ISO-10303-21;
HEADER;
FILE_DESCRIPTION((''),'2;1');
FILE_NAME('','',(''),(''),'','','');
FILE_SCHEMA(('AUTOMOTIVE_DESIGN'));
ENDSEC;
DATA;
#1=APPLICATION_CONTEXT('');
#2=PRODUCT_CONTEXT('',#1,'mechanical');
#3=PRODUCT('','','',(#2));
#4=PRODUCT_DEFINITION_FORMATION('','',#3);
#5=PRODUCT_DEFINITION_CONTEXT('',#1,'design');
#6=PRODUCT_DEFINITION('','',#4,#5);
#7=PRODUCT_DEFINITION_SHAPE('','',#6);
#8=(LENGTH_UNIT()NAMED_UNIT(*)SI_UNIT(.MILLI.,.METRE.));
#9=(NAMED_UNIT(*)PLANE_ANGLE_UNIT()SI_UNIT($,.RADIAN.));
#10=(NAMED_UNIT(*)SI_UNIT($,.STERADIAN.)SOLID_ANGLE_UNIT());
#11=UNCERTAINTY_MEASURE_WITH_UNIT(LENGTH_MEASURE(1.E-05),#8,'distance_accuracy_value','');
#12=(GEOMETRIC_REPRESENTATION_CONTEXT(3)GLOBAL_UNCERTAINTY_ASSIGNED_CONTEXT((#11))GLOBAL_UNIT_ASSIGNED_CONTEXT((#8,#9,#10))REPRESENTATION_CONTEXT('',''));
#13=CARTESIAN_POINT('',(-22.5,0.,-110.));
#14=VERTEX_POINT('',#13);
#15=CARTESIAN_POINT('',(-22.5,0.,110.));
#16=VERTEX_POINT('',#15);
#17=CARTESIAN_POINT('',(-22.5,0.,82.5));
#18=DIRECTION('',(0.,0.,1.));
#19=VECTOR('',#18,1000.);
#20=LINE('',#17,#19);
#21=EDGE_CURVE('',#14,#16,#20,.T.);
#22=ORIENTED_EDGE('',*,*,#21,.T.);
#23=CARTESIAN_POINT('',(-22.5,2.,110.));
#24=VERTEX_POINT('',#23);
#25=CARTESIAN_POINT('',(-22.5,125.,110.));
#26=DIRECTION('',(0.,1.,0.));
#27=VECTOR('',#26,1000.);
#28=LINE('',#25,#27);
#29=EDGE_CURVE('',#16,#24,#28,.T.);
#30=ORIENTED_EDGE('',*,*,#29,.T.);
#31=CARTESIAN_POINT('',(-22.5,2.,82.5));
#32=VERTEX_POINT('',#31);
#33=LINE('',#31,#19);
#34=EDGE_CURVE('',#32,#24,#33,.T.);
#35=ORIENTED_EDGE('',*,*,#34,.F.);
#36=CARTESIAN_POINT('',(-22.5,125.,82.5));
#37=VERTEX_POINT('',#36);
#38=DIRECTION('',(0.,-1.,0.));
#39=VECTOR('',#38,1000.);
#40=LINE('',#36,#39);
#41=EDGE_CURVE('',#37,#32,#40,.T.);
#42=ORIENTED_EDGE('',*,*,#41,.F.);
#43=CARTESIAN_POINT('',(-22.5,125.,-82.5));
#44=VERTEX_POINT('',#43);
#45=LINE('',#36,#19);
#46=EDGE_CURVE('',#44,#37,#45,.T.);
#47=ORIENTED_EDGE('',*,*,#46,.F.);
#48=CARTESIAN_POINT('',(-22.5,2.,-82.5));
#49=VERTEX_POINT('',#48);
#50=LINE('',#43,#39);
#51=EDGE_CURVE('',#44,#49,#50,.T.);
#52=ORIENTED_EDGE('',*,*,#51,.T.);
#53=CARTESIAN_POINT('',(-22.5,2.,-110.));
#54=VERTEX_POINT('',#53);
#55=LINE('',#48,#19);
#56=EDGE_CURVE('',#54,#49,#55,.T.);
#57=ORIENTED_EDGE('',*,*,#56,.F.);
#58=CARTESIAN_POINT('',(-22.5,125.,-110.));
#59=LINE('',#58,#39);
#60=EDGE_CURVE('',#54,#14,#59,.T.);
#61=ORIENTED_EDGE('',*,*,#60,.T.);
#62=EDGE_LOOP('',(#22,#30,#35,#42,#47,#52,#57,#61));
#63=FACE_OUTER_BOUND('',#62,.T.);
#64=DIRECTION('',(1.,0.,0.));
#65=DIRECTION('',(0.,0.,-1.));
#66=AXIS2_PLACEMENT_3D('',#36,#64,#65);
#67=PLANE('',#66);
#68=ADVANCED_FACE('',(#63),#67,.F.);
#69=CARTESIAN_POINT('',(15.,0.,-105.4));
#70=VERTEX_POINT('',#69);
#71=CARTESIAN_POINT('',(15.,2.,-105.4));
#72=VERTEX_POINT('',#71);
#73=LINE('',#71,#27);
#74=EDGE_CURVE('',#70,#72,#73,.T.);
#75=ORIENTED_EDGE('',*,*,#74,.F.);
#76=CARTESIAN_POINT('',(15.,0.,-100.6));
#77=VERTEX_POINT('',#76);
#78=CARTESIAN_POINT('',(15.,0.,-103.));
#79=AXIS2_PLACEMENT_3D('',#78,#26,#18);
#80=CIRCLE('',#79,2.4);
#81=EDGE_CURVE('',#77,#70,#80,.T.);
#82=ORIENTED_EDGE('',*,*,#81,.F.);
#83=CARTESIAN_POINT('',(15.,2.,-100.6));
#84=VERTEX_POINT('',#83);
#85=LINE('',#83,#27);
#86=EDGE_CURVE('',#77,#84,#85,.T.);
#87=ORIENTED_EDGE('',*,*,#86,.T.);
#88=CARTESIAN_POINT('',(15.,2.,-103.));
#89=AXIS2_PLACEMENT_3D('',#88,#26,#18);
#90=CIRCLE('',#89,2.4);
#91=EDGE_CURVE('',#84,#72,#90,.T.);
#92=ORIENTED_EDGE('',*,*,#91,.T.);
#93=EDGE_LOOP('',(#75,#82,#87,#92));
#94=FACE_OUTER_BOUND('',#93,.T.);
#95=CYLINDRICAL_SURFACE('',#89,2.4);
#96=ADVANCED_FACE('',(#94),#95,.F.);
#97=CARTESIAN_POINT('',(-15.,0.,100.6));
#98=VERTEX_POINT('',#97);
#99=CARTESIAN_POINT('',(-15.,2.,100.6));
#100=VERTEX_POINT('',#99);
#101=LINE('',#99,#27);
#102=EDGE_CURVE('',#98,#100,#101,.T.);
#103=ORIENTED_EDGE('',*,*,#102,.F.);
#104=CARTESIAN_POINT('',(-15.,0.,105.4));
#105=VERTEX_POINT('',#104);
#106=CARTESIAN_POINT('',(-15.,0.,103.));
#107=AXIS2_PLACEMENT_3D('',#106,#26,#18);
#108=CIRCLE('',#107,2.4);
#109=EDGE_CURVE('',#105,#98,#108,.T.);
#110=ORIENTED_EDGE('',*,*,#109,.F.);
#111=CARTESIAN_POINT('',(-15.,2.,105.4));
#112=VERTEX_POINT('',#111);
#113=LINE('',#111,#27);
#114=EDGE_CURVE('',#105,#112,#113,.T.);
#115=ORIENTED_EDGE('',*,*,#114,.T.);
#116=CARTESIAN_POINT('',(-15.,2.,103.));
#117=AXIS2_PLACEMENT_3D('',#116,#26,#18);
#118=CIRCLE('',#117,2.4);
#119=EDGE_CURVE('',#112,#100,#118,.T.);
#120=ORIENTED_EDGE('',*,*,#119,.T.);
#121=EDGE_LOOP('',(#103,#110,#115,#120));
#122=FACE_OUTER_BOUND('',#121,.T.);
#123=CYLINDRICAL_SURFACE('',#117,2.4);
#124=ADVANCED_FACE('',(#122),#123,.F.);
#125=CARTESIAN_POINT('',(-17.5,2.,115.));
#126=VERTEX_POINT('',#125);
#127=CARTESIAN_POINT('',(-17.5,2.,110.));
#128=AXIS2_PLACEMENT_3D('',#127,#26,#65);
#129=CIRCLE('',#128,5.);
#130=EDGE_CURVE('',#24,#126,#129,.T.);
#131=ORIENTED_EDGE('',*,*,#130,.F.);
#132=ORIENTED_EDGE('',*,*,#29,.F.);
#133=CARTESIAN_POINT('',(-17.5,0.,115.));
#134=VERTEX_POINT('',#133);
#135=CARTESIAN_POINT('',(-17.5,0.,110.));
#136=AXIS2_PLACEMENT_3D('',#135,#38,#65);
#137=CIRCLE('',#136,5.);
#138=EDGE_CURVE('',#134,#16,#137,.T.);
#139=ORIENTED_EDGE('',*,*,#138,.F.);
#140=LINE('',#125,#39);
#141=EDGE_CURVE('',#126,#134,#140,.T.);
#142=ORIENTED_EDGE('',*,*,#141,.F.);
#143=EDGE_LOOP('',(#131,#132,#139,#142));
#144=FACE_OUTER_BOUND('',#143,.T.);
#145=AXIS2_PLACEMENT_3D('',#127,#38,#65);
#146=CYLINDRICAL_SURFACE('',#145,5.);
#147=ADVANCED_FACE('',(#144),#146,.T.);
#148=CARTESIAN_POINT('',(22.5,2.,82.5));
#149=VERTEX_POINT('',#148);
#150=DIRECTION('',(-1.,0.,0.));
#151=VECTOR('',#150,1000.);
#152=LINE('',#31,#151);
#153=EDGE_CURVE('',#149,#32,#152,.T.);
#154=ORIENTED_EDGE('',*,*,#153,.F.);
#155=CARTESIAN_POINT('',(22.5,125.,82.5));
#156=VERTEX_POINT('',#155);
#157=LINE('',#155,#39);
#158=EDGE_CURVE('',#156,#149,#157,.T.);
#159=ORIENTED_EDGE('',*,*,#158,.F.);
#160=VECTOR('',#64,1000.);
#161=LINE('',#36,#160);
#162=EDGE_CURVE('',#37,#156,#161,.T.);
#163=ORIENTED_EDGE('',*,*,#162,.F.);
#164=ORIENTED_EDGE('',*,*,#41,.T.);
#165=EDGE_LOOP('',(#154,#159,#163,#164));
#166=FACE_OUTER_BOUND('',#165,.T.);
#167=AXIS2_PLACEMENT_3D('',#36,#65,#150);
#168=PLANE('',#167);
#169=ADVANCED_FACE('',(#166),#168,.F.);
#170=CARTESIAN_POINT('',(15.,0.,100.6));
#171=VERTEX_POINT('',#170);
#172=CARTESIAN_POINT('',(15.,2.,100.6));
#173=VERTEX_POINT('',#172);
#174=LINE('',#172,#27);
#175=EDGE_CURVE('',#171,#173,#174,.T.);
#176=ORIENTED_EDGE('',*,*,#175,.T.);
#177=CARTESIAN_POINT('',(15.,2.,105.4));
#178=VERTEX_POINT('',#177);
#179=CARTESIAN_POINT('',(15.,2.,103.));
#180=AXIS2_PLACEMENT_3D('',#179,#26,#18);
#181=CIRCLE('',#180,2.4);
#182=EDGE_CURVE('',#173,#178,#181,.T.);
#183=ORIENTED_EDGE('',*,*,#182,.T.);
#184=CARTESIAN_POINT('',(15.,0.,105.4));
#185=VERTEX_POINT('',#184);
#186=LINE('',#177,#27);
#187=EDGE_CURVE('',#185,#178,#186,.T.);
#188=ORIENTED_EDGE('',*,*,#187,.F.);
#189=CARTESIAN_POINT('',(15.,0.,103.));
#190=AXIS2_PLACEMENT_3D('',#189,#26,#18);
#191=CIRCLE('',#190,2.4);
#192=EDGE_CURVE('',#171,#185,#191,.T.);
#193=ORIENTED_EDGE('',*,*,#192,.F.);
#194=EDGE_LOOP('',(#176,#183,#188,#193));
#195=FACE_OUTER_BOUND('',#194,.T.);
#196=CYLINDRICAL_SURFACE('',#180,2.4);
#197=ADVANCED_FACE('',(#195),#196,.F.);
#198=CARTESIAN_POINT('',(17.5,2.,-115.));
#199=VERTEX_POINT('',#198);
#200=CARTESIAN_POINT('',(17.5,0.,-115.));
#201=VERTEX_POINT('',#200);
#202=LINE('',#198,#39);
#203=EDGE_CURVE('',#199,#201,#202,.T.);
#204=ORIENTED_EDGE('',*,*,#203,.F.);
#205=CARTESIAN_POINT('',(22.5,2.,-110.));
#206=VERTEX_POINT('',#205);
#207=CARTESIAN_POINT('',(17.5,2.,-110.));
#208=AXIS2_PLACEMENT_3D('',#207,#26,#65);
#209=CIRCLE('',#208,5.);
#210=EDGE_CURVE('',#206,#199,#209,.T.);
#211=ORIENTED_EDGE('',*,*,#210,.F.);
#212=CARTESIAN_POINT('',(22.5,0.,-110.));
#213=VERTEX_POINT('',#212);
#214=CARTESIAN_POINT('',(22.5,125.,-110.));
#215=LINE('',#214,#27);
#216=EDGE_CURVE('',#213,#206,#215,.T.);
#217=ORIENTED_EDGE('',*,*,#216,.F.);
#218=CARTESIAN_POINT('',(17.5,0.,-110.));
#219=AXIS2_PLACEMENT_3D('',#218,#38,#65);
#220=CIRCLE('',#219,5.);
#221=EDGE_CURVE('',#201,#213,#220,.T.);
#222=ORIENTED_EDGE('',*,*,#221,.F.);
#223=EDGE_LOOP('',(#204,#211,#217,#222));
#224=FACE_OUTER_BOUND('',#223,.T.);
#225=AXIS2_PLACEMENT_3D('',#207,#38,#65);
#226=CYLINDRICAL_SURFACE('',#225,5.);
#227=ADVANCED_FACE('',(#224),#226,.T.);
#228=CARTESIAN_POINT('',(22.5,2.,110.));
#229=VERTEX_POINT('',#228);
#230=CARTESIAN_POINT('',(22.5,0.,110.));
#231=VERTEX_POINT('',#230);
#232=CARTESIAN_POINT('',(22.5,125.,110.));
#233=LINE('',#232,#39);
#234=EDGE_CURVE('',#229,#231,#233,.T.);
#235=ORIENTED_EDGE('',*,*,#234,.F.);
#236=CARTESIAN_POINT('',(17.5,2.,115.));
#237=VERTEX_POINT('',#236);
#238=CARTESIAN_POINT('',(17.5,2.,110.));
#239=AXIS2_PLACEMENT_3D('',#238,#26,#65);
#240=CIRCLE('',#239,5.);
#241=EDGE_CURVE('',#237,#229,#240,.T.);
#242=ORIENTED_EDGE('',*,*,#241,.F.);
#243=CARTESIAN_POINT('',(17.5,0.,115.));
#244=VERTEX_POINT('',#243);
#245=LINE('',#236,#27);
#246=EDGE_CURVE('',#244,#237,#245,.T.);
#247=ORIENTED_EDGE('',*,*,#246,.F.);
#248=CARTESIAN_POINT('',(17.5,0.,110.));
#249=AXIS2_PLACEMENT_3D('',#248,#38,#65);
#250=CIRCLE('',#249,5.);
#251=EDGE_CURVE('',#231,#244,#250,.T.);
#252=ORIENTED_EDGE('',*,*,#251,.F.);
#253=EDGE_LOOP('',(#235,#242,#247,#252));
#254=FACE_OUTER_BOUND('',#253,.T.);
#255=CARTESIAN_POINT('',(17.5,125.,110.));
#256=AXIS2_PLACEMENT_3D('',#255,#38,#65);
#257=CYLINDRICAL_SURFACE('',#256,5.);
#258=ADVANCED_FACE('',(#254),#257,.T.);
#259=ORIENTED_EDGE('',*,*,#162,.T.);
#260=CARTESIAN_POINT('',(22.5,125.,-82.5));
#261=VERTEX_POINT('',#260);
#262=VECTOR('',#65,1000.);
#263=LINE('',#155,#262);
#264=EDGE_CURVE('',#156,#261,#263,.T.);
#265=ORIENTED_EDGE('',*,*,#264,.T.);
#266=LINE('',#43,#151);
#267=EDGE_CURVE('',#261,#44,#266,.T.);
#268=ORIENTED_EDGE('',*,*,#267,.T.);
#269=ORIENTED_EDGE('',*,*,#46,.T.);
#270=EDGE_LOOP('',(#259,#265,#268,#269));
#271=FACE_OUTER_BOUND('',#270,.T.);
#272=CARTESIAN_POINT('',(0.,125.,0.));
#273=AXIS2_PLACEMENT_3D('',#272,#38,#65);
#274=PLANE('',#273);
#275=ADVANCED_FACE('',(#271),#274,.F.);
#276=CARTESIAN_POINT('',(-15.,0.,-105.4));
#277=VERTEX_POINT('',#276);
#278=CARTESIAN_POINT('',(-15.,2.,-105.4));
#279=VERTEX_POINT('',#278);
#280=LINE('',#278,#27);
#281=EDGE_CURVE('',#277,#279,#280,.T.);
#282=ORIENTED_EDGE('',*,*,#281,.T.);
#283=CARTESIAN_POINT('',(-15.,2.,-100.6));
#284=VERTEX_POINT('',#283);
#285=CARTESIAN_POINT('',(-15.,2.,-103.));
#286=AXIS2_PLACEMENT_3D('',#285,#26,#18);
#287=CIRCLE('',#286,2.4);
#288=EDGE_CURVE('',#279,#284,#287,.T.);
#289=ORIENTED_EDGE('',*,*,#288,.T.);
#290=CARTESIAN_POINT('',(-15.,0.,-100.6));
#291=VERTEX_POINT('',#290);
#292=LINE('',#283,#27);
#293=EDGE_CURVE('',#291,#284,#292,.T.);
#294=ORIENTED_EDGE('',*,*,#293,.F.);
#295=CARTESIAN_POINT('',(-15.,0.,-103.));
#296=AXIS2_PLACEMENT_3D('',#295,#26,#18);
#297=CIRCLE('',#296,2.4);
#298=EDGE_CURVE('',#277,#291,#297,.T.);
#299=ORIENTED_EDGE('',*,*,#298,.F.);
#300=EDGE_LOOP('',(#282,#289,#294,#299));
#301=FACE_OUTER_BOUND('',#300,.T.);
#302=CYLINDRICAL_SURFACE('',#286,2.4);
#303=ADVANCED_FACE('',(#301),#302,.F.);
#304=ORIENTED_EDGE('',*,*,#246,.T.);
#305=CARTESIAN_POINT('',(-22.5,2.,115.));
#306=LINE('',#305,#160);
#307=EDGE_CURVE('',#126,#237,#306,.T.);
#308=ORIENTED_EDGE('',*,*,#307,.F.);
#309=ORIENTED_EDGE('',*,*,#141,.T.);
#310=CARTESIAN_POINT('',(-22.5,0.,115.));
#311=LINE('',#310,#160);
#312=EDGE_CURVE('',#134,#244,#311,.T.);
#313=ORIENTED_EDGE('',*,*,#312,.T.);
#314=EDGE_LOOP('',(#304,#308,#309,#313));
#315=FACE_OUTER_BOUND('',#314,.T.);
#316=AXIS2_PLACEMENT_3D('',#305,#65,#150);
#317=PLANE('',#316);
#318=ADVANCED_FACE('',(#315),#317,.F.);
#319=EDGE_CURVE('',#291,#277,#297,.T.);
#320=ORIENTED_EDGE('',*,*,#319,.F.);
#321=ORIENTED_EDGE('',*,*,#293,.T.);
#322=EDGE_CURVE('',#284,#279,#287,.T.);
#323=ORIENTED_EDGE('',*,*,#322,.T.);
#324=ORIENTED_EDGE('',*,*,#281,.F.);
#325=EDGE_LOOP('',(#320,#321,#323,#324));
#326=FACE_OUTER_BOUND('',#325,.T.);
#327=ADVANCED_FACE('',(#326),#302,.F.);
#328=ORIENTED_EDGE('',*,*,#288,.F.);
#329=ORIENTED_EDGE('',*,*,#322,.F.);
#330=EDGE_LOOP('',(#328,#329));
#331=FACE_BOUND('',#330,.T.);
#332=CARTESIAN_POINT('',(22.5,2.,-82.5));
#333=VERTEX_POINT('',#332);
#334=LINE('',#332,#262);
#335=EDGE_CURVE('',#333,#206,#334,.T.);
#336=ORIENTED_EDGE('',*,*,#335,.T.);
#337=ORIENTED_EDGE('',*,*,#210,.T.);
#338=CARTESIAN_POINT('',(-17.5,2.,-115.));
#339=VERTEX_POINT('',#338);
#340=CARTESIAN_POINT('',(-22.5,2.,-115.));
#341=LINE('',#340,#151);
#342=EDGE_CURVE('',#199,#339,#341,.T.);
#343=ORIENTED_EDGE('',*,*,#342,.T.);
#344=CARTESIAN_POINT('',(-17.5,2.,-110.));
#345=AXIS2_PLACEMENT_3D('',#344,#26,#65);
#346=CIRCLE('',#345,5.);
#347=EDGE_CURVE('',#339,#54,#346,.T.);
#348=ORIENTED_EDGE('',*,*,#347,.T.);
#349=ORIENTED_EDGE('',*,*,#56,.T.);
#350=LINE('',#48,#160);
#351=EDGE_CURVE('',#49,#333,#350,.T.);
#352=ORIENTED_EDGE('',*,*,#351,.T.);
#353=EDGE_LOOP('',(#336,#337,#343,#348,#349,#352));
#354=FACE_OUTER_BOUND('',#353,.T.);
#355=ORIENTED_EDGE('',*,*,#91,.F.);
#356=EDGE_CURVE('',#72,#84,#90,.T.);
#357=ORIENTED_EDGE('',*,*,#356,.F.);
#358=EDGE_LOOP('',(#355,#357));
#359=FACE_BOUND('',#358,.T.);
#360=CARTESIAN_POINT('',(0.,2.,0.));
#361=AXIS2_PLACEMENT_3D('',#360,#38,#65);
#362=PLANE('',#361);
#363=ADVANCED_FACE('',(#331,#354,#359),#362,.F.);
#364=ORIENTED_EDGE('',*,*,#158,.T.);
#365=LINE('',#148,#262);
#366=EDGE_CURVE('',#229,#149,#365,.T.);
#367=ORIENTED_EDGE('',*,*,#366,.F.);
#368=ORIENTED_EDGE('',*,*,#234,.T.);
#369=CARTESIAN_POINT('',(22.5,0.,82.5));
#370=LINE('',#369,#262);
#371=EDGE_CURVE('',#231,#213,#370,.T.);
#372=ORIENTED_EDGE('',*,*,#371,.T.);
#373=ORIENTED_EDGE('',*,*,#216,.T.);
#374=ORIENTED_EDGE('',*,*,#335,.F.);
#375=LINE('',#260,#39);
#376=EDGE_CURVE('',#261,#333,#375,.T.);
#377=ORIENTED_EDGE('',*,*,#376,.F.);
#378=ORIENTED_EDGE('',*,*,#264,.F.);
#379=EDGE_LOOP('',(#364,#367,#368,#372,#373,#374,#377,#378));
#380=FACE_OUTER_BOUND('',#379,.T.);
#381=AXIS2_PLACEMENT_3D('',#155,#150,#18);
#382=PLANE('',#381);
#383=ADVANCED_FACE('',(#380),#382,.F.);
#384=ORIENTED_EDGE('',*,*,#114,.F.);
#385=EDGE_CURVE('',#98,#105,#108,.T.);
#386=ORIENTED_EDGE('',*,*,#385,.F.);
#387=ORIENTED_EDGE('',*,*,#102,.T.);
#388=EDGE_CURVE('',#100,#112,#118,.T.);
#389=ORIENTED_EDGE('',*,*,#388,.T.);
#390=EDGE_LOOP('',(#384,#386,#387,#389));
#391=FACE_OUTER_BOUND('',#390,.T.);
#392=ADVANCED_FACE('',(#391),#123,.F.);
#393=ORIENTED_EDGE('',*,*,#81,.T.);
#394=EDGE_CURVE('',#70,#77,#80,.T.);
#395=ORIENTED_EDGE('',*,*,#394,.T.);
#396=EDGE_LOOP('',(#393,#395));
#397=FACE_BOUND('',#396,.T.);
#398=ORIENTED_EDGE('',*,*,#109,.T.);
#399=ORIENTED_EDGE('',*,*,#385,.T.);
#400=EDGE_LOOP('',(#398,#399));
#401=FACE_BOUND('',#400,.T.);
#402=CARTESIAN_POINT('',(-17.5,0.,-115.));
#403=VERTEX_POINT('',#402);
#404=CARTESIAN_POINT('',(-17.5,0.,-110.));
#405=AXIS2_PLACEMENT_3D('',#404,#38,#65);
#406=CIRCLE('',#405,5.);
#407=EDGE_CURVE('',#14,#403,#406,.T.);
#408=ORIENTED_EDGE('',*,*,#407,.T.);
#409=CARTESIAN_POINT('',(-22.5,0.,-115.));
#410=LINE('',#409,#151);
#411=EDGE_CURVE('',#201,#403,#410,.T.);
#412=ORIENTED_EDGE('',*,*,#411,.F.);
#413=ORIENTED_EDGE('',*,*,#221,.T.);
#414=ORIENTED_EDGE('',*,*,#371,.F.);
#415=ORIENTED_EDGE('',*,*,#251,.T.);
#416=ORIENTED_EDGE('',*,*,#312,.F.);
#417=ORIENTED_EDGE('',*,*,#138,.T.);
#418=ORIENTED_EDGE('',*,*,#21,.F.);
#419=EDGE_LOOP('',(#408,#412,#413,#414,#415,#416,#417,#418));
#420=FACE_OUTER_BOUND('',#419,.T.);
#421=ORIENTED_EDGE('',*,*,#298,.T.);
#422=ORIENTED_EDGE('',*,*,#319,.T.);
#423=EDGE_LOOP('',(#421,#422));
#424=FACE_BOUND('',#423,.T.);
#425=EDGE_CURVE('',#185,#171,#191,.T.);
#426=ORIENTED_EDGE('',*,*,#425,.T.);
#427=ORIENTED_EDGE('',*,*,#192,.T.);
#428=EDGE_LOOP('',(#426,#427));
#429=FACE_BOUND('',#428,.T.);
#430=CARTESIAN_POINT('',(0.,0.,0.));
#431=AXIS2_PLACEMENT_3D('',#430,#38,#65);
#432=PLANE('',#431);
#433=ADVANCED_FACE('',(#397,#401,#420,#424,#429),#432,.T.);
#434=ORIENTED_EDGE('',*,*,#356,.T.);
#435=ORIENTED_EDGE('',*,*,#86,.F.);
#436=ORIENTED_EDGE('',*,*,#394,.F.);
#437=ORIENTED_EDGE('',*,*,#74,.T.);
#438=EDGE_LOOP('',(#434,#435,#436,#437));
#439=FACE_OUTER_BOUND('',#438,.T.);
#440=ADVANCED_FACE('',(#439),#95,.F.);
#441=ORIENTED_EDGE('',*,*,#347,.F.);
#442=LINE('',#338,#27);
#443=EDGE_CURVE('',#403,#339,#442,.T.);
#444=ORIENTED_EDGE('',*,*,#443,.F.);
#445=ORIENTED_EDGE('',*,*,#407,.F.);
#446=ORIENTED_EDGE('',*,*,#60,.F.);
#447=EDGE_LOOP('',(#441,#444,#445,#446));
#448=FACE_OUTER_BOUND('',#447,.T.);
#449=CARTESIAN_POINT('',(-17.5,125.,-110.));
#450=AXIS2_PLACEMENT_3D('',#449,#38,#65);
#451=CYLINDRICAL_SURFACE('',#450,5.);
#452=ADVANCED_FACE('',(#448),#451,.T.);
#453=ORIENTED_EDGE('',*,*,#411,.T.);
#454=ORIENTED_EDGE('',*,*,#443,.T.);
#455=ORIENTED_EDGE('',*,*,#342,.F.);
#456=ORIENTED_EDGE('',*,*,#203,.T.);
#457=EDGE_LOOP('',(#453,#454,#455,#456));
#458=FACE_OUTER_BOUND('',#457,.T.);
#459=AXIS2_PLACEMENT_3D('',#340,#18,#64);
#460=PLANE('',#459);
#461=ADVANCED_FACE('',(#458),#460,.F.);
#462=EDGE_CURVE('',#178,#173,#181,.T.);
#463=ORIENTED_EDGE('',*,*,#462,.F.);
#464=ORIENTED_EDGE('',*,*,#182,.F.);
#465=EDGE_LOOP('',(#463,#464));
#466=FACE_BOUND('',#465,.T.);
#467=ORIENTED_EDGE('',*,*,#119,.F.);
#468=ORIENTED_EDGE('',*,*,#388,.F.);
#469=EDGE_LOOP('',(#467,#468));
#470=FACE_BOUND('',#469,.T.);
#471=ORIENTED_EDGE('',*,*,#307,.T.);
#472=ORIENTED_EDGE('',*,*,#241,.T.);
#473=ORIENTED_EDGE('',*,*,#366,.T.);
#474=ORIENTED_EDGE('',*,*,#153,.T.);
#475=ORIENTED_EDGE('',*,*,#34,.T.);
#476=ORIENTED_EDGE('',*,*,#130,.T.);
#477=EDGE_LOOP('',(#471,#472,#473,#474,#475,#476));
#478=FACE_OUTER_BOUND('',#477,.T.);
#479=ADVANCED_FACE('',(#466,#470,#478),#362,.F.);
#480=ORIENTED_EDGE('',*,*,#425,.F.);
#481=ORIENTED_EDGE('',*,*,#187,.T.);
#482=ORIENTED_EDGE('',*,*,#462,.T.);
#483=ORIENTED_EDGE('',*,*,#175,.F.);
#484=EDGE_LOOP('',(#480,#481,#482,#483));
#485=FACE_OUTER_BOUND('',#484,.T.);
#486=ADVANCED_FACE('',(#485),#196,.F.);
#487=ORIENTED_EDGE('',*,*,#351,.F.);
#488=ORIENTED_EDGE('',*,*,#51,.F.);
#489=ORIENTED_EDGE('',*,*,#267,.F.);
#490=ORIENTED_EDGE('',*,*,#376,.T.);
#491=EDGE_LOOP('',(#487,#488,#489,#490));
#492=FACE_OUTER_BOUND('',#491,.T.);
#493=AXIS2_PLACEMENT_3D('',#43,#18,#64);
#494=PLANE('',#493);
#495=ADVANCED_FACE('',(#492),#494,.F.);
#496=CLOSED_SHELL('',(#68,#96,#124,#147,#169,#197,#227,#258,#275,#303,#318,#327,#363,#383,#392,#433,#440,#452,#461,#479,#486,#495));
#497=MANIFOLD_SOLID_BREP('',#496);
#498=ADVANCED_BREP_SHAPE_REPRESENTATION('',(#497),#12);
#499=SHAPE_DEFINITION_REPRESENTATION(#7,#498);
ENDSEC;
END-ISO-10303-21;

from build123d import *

# Parameters (mm, degrees)
SKETCH_1_W         = 45
SKETCH_1_H         = 165
EXTRUDE_1_DEPTH    = 125
SKETCH_3_W         = 45
SKETCH_3_H         = 32.5
EXTRUDE_2_DEPTH    = 2
HOLE_WIZARD_M4_1_D = 4.8
FILLET_1_R         = 5


with BuildPart() as part:
    # 草图1 → 凸台-拉伸1 (new body)
    with BuildSketch(Plane(origin=(0, 0, 0), x_dir=(1, 0, 0), z_dir=(0, 1, 0))):
        Rectangle(SKETCH_1_W, SKETCH_1_H)
    extrude(amount=EXTRUDE_1_DEPTH)

    # 草图3 → 凸台-拉伸2 (add)
    with BuildSketch(Plane(origin=(0, 0, 0), x_dir=(1, 0, 0), z_dir=(0, 1, 0))):
        with Locations((0, 98.75)):
            Rectangle(SKETCH_3_W, SKETCH_3_H)
        with Locations((0, -98.75)):
            Rectangle(SKETCH_3_W, SKETCH_3_H)
    extrude(amount=EXTRUDE_2_DEPTH)

    # M4 间隙孔1 (through all)
    with Locations(Plane(origin=(0, 2, 0), x_dir=(1, 0, 0), z_dir=(0, 1, 0))):
        with Locations((-15, 103), (15, 103), (15, -103), (-15, -103)):
            Hole(HOLE_WIZARD_M4_1_D / 2)

    # 圆角1
    fillet_1_edges = [part.edges().sort_by_distance(p)[0] for p in [
        (-22.5, 1, -115),
        (22.5, 1, -115),
        (-22.5, 1, 115),
        (22.5, 1, 115),
    ]]
    fillet(fillet_1_edges, radius=FILLET_1_R)


solid = part.part
